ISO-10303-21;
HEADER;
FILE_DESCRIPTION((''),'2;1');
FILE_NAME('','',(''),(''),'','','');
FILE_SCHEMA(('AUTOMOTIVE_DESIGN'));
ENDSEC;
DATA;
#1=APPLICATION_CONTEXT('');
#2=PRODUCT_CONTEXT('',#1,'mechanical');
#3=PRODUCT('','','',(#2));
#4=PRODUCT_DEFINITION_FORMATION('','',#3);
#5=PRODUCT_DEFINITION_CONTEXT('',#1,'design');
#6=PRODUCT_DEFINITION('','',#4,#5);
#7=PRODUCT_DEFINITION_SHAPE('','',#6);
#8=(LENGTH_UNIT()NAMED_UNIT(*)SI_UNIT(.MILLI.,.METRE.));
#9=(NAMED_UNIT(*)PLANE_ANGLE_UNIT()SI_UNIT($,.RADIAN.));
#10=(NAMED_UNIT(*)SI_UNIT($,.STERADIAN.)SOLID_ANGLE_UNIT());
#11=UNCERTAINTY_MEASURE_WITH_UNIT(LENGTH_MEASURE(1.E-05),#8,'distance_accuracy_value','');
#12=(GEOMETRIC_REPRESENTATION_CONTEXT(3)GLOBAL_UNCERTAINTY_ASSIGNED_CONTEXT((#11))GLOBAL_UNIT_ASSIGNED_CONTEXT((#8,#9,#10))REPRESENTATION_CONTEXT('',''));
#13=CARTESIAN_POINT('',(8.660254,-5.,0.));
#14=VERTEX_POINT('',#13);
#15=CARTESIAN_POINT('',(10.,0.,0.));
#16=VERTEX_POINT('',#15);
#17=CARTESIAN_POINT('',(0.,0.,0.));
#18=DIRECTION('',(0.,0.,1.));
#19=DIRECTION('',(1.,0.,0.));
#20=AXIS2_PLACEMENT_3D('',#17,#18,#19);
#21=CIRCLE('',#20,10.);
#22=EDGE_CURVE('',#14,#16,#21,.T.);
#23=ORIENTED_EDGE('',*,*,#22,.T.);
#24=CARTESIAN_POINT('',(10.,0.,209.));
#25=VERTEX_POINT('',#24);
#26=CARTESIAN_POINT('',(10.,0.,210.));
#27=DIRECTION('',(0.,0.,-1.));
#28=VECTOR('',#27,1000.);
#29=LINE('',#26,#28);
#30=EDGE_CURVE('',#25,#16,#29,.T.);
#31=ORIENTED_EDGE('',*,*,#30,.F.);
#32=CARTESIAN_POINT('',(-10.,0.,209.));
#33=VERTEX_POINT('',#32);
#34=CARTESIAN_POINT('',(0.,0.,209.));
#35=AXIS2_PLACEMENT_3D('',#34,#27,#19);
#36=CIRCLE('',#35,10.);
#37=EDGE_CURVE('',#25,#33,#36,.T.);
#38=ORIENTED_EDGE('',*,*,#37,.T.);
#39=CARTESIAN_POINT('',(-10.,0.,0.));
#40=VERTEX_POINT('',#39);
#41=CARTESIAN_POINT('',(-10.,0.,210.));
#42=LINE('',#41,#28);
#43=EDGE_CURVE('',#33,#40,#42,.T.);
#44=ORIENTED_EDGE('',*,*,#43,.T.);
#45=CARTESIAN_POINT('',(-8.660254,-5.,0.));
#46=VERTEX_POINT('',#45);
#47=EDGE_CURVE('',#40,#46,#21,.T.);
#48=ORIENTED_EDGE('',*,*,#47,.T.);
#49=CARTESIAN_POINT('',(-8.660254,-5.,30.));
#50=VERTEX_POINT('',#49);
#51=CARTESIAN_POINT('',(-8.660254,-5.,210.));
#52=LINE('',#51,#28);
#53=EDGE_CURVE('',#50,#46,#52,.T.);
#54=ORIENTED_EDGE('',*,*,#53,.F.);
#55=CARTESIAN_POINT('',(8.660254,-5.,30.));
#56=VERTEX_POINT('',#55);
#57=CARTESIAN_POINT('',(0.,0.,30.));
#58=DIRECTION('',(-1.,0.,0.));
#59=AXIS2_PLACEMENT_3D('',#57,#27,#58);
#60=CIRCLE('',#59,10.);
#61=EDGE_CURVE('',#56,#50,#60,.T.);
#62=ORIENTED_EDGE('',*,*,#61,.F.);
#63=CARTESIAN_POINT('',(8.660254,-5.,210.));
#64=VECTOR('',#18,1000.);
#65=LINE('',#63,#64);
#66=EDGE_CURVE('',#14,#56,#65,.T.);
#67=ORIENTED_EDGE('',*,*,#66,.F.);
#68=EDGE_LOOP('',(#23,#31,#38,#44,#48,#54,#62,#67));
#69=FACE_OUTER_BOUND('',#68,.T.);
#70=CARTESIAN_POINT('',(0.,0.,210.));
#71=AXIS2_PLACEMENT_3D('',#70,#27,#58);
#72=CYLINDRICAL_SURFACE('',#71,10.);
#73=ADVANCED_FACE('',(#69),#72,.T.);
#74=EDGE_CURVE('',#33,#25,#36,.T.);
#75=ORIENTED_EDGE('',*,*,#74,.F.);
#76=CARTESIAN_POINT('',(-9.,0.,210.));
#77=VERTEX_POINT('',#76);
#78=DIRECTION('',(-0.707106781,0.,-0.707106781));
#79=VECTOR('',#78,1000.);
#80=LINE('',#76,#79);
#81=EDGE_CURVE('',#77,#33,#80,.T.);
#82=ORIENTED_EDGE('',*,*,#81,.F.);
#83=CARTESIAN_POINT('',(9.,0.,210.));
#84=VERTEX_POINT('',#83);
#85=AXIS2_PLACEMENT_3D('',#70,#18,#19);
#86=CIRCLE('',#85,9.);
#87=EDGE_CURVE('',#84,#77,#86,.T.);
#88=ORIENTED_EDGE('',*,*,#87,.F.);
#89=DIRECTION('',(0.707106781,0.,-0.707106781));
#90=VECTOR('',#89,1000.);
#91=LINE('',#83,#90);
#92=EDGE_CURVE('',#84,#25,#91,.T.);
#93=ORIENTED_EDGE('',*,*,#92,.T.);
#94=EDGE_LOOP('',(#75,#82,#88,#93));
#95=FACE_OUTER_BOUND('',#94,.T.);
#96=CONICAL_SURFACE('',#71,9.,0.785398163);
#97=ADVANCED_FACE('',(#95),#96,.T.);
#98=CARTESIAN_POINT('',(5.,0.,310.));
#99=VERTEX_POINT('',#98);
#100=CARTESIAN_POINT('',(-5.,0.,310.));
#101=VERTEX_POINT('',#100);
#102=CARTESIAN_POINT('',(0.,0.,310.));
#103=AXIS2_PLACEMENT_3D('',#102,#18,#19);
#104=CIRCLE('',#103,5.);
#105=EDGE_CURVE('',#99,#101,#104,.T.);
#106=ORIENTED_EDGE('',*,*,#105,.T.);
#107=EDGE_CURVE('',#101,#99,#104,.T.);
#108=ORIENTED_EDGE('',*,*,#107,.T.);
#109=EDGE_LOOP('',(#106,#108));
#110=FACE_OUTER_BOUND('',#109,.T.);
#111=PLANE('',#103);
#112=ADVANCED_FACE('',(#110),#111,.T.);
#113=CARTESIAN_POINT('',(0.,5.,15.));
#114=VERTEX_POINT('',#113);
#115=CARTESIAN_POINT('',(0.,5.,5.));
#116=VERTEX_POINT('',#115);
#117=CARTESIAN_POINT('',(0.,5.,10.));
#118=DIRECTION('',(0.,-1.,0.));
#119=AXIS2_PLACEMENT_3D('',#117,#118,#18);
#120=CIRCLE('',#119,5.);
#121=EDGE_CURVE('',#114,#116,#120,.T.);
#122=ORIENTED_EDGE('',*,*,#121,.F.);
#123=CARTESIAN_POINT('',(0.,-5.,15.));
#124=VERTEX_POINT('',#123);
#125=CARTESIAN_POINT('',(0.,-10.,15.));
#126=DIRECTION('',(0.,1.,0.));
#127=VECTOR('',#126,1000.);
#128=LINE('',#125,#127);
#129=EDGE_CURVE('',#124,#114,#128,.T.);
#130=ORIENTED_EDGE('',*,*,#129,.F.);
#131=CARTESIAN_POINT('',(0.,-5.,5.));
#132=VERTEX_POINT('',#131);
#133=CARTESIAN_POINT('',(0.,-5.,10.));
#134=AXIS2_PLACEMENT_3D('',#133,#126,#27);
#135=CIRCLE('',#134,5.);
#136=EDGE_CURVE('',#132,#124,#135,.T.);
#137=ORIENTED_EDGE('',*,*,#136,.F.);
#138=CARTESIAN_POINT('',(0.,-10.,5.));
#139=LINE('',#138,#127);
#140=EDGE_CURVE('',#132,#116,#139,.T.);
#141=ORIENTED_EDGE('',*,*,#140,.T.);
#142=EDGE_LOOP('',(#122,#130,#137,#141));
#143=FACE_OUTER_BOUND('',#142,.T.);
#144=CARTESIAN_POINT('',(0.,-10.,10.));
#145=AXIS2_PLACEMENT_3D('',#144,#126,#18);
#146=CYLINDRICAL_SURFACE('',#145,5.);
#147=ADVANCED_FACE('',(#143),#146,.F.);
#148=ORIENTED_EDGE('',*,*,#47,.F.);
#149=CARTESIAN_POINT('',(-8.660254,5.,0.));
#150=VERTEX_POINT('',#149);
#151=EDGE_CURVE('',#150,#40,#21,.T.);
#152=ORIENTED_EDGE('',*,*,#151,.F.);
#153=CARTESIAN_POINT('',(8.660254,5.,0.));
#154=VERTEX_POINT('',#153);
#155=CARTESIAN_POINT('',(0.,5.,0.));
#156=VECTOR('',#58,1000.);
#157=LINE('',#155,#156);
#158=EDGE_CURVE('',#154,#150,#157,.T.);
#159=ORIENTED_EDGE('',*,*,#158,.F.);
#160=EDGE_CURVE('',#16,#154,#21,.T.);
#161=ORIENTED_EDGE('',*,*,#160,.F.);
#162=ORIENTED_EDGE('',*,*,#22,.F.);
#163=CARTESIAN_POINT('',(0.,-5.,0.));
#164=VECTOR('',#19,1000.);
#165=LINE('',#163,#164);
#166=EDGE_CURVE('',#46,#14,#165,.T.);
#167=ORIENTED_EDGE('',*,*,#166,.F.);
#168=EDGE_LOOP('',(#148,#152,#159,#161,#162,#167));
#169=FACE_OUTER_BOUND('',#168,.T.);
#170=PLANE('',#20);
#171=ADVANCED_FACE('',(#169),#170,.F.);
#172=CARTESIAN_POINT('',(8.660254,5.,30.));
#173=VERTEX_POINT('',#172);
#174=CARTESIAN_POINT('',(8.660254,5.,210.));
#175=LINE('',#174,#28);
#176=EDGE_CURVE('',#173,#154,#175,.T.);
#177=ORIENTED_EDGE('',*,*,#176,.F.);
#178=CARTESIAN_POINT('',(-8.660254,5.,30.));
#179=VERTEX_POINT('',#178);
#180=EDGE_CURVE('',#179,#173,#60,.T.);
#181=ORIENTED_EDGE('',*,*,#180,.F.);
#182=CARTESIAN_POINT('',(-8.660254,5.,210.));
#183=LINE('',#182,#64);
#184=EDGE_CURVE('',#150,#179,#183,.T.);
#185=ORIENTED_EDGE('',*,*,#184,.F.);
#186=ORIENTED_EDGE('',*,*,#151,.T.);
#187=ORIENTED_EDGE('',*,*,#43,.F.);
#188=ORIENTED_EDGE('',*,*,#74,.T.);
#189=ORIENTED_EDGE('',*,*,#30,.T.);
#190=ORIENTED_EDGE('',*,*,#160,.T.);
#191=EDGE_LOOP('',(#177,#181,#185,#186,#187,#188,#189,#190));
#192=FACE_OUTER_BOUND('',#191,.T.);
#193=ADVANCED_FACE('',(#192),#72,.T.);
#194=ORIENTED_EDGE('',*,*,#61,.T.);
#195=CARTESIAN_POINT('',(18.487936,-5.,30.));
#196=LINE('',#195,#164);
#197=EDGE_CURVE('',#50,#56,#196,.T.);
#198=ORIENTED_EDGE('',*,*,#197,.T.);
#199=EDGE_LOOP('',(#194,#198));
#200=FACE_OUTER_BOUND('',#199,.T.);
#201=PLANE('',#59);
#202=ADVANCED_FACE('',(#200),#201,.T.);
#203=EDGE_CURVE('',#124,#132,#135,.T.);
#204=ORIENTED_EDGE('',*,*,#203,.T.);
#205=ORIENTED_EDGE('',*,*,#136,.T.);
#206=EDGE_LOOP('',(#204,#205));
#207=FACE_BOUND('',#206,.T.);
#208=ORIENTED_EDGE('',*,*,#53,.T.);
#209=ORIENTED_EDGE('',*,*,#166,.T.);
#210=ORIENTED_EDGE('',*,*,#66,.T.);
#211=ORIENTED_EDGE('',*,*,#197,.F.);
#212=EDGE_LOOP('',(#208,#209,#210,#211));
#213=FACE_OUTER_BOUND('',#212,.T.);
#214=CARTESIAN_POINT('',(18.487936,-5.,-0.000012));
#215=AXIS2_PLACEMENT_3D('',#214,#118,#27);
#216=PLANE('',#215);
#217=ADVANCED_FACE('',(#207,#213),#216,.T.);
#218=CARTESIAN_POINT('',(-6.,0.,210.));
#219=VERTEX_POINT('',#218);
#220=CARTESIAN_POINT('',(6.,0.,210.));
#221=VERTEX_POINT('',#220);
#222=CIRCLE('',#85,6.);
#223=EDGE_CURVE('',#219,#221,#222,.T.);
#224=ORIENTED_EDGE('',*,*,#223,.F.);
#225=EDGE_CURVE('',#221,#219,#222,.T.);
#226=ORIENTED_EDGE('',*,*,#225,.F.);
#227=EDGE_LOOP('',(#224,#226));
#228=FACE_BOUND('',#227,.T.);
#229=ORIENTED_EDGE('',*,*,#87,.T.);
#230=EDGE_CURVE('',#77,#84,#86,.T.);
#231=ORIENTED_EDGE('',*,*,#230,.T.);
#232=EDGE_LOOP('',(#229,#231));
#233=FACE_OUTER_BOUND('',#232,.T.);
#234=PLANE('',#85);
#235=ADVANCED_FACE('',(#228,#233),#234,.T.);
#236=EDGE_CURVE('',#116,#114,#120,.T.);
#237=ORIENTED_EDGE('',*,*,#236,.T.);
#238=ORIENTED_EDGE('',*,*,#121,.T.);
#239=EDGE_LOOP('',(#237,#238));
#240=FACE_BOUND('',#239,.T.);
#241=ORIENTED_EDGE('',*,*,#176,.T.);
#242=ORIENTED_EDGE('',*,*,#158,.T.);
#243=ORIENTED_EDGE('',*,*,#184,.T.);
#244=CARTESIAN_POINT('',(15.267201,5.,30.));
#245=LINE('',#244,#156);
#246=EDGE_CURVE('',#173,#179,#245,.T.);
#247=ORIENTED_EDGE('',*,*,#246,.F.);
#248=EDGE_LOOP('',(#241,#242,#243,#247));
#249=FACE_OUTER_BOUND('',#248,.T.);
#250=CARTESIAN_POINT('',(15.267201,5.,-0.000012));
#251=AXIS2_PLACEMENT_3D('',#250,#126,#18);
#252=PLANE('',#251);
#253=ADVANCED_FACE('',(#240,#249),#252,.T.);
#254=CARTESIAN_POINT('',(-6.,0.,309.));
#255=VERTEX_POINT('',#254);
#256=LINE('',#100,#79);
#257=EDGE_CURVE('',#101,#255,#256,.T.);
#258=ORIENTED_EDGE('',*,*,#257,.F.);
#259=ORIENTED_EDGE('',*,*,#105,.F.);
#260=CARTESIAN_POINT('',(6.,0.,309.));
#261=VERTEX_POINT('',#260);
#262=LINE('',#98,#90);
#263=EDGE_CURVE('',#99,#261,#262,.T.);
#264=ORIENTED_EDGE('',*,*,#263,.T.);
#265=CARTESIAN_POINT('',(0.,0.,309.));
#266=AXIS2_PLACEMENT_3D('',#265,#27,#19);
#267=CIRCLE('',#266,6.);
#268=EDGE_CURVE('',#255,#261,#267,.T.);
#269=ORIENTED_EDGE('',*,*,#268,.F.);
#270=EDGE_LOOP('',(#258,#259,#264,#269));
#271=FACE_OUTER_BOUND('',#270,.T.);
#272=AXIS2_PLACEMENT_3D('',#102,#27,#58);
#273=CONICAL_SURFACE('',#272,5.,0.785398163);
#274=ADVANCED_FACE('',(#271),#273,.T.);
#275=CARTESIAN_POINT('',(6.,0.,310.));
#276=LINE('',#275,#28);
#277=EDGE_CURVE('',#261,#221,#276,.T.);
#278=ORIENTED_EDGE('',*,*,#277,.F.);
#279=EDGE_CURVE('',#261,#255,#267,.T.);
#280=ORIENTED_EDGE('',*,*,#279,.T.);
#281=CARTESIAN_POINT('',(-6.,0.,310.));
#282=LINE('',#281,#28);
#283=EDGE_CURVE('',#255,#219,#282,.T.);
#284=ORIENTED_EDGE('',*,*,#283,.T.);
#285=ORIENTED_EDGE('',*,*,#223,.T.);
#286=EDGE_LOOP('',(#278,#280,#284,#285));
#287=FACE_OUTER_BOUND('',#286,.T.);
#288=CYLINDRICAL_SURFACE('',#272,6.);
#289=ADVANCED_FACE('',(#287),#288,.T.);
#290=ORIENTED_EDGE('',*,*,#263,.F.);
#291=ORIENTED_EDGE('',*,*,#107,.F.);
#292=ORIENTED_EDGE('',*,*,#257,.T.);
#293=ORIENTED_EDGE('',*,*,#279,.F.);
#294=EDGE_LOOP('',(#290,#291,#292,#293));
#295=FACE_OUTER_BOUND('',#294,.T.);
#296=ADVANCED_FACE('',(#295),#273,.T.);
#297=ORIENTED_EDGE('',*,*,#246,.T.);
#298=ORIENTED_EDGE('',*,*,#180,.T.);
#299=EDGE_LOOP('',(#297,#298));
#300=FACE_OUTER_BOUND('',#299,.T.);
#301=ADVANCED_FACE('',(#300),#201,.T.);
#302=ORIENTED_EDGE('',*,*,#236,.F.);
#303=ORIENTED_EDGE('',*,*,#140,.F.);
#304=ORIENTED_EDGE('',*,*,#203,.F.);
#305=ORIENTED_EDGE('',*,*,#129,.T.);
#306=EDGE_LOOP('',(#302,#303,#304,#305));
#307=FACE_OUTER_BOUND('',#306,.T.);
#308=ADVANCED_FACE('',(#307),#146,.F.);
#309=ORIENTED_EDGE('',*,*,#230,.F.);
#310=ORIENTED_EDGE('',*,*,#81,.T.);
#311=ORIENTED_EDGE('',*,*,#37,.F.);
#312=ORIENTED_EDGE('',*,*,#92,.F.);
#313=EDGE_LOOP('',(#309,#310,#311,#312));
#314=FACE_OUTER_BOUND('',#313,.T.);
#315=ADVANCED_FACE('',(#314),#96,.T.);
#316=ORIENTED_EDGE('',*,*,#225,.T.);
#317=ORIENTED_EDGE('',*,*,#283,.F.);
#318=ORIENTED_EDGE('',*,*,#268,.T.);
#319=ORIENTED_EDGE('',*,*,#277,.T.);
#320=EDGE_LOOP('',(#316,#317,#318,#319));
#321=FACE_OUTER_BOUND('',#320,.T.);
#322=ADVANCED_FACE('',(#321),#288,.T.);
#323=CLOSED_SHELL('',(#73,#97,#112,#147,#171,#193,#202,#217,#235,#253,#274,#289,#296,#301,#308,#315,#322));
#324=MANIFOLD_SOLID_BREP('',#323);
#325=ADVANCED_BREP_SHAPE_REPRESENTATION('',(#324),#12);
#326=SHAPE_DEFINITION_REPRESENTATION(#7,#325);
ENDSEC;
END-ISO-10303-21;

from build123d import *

# Parameters (mm, degrees)
SKETCH1_R               = 10
BOSS_EXTRUDE1_DEPTH     = 210
CUT_EXTRUDE1_DEPTH      = 211.475651798
CUT_EXTRUDE1_DEPTH_BACK = 211.475651798
SKETCH2_R               = 5
CUT_EXTRUDE2_DEPTH      = 211.475651908
CUT_EXTRUDE2_DEPTH_BACK = 30
SKETCH3_W               = 38.012097267
SKETCH3_H               = 10.508452135
SKETCH3_W_2             = 32.719606191
SKETCH3_H_2             = 9.885466079
SKETCH4_R               = 6
BOSS_EXTRUDE2_DEPTH     = 100
CHAMFER1_SIZE           = 1


with BuildPart() as part:
    # Sketch1 → Boss-Extrude1 (new body)
    with BuildSketch(Plane.XY):
        Circle(SKETCH1_R)
    extrude(amount=BOSS_EXTRUDE1_DEPTH)

    # Sketch2 → Cut-Extrude1 (cut, two sides: drawn at the far end of the back side and taken through both)
    with BuildSketch(Plane(origin=(0, 0, 0), x_dir=(1, 0, 0), z_dir=(0, 1, 0)).offset(-CUT_EXTRUDE1_DEPTH_BACK)):
        with Locations(Location((0, -10, 0), (0, 0, 270))):
            Circle(SKETCH2_R)
    extrude(amount=CUT_EXTRUDE1_DEPTH + CUT_EXTRUDE1_DEPTH_BACK, mode=Mode.SUBTRACT)

    # Sketch3 → Cut-Extrude2 (cut, two sides: drawn at the far end of the back side and taken through both)
    with BuildSketch(Plane(origin=(0, 0, 0), x_dir=(-1, 0, 0), z_dir=(0, 0, -1)).offset(-CUT_EXTRUDE2_DEPTH_BACK)):
        with Locations((0.51811282, -10.254226067)):
            Rectangle(SKETCH3_W, SKETCH3_H)
        with Locations((1.092602531, 9.94273304)):
            Rectangle(SKETCH3_W_2, SKETCH3_H_2)
    extrude(amount=CUT_EXTRUDE2_DEPTH + CUT_EXTRUDE2_DEPTH_BACK, mode=Mode.SUBTRACT)

    # Sketch4 → Boss-Extrude2 (add)
    with BuildSketch(Plane.XY.offset(210)):
        Circle(SKETCH4_R)
    extrude(amount=BOSS_EXTRUDE2_DEPTH)

    # Chamfer1
    chamfer1_edges = [part.edges().sort_by_distance(p)[0] for p in [
        (-10, 0, 210),
        (-6, 0, 310),
    ]]
    chamfer(chamfer1_edges, length=CHAMFER1_SIZE)


solid = part.part
